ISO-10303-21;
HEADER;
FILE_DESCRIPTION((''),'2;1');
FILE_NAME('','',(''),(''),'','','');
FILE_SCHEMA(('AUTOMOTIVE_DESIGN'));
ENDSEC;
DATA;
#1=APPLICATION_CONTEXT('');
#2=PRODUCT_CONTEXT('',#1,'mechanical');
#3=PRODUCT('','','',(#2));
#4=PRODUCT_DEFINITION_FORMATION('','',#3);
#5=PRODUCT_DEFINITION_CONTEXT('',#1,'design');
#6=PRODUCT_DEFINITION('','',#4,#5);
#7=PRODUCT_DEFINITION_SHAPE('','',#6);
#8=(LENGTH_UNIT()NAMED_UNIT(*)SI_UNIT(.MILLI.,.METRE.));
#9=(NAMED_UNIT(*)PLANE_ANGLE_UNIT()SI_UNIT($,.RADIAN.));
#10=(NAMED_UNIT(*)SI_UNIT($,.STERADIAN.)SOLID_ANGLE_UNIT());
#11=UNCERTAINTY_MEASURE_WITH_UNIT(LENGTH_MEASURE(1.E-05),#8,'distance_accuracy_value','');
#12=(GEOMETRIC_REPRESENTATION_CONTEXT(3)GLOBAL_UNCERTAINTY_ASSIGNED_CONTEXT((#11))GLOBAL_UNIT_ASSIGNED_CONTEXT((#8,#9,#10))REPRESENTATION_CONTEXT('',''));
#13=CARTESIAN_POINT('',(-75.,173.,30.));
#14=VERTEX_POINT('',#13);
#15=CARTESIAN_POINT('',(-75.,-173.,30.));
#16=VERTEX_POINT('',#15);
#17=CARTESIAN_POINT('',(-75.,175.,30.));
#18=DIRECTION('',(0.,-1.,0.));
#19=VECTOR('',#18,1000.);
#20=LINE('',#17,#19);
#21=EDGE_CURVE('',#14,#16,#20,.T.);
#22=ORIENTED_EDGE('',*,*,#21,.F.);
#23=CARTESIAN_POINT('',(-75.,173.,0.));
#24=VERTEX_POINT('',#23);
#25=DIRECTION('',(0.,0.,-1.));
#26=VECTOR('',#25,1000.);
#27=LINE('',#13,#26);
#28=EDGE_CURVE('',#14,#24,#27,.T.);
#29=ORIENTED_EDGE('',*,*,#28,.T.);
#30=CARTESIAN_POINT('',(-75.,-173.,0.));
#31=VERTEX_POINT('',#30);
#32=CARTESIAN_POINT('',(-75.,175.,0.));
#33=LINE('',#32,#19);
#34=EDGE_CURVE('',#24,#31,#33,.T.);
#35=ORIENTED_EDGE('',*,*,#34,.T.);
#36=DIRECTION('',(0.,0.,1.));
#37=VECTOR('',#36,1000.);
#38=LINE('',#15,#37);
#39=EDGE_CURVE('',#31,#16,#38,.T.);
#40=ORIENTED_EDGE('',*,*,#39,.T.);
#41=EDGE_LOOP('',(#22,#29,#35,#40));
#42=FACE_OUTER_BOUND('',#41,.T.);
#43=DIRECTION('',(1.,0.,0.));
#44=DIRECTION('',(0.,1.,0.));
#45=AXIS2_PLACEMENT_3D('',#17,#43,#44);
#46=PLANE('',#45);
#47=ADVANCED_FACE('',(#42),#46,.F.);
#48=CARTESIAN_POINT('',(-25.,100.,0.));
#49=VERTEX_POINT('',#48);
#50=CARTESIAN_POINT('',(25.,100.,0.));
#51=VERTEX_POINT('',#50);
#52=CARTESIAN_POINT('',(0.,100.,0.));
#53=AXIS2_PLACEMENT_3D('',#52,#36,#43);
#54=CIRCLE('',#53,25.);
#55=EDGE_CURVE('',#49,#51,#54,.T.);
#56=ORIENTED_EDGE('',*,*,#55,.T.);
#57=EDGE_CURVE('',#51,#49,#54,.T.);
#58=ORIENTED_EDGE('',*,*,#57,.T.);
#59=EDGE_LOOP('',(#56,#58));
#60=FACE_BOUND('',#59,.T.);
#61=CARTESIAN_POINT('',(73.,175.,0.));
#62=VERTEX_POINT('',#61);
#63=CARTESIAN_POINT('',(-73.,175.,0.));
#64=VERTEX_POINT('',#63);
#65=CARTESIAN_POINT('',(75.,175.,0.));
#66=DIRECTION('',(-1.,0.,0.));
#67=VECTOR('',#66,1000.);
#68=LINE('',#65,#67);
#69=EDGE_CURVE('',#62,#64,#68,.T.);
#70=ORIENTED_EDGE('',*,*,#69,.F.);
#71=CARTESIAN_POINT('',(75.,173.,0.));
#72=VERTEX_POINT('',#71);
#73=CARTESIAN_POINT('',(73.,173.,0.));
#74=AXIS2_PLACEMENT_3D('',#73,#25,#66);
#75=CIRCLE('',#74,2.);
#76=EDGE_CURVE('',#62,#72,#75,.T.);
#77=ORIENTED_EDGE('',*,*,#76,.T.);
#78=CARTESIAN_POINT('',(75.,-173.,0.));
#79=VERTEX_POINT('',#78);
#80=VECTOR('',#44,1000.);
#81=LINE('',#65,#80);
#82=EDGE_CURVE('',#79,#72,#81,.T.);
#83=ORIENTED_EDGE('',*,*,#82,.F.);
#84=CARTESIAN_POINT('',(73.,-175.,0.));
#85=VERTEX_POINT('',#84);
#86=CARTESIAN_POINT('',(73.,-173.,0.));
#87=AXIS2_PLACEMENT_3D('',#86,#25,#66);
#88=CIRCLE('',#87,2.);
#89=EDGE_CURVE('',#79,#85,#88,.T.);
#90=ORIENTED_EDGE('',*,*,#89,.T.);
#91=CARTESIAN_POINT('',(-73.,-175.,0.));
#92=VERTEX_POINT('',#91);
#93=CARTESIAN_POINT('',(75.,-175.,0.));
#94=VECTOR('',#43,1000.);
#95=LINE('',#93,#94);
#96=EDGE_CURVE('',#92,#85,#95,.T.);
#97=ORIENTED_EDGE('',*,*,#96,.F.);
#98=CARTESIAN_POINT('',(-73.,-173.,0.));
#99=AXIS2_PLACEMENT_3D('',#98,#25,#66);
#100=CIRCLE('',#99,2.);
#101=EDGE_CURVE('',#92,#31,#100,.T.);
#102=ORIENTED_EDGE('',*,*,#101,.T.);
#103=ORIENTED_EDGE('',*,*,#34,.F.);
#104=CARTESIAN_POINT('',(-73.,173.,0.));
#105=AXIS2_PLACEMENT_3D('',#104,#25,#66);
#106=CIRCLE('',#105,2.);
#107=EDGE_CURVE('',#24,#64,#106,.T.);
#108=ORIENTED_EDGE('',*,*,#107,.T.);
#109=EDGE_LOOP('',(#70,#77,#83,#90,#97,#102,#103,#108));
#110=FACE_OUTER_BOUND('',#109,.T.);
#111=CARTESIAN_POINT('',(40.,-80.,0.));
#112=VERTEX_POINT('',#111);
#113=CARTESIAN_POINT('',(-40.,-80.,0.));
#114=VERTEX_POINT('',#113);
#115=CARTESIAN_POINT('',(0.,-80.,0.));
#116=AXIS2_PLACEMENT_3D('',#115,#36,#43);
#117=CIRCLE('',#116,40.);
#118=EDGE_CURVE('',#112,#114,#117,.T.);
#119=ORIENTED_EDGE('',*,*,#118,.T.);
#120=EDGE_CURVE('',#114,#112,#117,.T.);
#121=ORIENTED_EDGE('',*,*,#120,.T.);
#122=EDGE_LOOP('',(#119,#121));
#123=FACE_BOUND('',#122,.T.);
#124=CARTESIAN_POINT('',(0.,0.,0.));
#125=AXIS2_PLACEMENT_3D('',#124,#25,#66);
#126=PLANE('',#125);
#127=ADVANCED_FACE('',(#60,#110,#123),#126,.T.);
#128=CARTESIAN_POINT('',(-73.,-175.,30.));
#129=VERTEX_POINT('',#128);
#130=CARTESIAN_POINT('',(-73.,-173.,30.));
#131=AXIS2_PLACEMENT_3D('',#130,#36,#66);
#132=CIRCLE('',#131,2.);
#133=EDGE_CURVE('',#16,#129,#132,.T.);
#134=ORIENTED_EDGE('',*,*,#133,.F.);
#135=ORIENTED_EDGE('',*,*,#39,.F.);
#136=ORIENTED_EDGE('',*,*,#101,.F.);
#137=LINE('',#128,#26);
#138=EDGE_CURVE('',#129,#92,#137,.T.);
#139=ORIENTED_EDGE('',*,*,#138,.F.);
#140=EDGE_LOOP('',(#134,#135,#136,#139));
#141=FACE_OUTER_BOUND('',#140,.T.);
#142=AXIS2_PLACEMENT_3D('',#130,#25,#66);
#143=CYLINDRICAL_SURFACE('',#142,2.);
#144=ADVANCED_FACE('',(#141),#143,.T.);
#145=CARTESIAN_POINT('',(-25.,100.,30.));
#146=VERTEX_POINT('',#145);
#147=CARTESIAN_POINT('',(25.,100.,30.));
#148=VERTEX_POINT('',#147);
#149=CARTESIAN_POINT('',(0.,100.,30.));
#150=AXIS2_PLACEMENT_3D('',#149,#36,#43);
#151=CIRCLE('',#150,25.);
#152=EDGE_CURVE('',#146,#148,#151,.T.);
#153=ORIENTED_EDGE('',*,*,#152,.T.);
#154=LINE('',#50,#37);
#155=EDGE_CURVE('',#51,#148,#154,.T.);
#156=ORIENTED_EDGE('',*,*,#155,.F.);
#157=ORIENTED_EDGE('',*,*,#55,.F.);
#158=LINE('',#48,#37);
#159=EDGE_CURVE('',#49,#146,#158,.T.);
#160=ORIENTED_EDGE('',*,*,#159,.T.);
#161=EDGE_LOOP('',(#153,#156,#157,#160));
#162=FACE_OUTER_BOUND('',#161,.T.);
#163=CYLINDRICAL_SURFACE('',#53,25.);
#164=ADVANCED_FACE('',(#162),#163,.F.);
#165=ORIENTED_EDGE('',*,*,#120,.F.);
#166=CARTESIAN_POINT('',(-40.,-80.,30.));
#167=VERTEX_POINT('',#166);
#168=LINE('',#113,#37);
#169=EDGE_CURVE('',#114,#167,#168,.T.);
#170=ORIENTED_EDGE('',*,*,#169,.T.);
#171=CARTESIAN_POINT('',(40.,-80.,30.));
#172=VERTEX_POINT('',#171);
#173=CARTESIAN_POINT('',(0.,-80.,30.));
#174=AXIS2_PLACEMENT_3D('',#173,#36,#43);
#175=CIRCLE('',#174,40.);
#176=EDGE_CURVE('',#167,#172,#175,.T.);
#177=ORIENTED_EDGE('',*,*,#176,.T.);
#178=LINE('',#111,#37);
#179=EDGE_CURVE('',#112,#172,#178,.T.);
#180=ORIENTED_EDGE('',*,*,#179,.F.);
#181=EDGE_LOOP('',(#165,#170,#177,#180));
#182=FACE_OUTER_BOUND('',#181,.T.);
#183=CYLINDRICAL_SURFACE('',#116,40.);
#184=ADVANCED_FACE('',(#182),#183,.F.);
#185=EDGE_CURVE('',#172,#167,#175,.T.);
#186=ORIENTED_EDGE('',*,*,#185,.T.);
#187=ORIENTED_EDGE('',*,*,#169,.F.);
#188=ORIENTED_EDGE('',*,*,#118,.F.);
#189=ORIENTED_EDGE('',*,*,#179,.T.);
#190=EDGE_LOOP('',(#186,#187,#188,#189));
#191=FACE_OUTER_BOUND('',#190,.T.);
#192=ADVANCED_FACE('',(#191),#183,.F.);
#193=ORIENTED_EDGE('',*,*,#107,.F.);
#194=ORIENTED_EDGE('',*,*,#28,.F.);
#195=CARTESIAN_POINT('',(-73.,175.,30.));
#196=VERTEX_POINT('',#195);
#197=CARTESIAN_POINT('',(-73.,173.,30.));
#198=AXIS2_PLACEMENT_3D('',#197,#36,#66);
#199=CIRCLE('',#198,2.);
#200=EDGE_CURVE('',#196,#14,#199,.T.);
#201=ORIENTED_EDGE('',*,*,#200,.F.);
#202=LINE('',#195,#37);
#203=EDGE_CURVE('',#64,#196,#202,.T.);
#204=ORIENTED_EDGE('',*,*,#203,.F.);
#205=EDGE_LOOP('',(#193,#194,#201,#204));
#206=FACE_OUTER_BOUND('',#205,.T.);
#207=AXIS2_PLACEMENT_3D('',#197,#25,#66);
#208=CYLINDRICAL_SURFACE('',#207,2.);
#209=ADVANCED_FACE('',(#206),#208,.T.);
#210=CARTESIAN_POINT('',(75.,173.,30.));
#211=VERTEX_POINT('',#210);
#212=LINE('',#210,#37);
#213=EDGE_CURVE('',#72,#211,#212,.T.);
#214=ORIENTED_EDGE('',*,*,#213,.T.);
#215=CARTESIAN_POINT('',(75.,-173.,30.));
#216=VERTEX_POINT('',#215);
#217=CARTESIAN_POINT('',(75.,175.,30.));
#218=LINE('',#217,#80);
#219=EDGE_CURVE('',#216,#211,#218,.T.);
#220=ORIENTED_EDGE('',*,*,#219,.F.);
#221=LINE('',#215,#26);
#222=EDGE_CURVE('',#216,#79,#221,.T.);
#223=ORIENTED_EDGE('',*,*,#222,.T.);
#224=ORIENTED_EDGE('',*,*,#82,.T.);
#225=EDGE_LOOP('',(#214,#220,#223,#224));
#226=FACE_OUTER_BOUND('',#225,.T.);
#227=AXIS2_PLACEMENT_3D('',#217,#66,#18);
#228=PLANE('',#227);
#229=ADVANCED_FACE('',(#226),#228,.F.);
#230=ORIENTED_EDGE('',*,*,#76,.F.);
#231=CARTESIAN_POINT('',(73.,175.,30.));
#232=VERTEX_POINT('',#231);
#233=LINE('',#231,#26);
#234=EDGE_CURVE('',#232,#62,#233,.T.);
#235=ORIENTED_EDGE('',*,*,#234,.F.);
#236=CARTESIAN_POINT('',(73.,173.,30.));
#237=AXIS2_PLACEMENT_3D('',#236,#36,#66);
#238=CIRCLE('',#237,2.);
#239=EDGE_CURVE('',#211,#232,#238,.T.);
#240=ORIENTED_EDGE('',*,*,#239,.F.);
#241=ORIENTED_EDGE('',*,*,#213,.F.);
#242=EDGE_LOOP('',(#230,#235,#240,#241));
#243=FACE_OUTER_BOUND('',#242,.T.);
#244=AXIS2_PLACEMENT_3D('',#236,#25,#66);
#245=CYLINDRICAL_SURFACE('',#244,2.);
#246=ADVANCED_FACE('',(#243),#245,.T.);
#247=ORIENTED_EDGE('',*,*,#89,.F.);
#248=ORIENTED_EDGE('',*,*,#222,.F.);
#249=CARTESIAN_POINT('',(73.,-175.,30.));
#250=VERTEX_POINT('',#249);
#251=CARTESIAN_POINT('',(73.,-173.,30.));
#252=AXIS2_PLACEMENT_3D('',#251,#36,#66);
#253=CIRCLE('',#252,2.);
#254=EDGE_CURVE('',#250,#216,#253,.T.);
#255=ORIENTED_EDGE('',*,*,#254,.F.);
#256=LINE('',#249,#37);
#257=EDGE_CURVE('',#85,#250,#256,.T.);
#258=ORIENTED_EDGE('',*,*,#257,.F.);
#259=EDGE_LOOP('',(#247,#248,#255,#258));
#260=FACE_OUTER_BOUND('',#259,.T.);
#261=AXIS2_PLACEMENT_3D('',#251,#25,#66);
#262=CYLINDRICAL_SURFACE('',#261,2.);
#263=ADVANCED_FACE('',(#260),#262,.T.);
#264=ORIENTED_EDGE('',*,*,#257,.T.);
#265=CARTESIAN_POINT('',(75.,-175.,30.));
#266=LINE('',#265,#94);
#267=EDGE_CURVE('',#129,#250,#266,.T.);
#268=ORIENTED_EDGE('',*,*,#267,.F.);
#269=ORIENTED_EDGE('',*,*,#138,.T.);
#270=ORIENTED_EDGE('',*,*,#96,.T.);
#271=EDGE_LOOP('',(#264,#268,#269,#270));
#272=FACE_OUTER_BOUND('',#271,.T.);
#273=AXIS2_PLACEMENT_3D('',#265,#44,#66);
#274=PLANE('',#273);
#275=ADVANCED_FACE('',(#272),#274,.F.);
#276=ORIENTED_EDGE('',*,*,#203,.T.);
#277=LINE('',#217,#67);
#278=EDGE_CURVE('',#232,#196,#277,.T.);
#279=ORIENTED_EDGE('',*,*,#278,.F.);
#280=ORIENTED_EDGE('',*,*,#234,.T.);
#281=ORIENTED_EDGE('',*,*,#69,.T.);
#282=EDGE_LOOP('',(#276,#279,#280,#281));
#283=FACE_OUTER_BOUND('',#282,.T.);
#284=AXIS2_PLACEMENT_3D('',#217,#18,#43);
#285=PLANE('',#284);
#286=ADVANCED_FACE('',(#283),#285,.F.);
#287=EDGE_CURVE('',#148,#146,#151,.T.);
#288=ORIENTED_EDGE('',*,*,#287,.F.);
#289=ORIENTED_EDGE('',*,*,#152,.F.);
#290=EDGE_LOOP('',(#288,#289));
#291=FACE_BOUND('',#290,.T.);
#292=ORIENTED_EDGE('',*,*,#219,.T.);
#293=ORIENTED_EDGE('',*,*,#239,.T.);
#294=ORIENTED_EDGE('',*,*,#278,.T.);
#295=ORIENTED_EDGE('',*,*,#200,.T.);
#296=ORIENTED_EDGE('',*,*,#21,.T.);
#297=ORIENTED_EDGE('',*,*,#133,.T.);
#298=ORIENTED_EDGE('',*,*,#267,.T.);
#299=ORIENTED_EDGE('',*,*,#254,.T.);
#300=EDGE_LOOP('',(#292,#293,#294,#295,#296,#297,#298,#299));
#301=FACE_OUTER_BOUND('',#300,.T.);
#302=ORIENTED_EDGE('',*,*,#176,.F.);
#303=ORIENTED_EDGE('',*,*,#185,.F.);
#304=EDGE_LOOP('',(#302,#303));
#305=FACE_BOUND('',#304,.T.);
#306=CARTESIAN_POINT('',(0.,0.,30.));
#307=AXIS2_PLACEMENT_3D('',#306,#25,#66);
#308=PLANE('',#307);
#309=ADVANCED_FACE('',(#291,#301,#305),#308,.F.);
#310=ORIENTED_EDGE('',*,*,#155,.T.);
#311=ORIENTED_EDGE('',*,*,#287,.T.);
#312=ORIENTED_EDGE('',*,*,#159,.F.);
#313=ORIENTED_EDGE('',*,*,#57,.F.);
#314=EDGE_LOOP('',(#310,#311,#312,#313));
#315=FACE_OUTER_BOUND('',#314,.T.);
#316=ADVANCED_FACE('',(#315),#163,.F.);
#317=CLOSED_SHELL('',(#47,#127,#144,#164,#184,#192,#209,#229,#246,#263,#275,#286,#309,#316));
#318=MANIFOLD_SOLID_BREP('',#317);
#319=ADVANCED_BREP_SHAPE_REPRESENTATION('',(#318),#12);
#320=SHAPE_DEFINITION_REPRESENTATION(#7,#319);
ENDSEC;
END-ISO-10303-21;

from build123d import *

# Parameters (mm, degrees)
SKETCH1_W           = 150
SKETCH1_H           = 350
BOSS_EXTRUDE1_DEPTH = 30
SKETCH2_R           = 25
SKETCH2_R_2         = 40
CUT_EXTRUDE1_DEPTH  = 30
FILLET1_R           = 2


with BuildPart() as part:
    # Sketch1 → Boss-Extrude1 (new body)
    with BuildSketch(Plane.XY):
        Rectangle(SKETCH1_W, SKETCH1_H)
    extrude(amount=BOSS_EXTRUDE1_DEPTH)

    # Sketch2 → Cut-Extrude1 (cut)
    with BuildSketch(Plane.XY.offset(30)):
        with Locations((0, 100)):
            Circle(SKETCH2_R)
        with Locations((0, -80)):
            Circle(SKETCH2_R_2)
    extrude(amount=-CUT_EXTRUDE1_DEPTH, mode=Mode.SUBTRACT)

    # Fillet1
    fillet1_edges = [part.edges().sort_by_distance(p)[0] for p in [
        (-75, 175, 15),
        (75, 175, 15),
        (75, -175, 15),
        (-75, -175, 15),
    ]]
    fillet(fillet1_edges, radius=FILLET1_R)


solid = part.part
